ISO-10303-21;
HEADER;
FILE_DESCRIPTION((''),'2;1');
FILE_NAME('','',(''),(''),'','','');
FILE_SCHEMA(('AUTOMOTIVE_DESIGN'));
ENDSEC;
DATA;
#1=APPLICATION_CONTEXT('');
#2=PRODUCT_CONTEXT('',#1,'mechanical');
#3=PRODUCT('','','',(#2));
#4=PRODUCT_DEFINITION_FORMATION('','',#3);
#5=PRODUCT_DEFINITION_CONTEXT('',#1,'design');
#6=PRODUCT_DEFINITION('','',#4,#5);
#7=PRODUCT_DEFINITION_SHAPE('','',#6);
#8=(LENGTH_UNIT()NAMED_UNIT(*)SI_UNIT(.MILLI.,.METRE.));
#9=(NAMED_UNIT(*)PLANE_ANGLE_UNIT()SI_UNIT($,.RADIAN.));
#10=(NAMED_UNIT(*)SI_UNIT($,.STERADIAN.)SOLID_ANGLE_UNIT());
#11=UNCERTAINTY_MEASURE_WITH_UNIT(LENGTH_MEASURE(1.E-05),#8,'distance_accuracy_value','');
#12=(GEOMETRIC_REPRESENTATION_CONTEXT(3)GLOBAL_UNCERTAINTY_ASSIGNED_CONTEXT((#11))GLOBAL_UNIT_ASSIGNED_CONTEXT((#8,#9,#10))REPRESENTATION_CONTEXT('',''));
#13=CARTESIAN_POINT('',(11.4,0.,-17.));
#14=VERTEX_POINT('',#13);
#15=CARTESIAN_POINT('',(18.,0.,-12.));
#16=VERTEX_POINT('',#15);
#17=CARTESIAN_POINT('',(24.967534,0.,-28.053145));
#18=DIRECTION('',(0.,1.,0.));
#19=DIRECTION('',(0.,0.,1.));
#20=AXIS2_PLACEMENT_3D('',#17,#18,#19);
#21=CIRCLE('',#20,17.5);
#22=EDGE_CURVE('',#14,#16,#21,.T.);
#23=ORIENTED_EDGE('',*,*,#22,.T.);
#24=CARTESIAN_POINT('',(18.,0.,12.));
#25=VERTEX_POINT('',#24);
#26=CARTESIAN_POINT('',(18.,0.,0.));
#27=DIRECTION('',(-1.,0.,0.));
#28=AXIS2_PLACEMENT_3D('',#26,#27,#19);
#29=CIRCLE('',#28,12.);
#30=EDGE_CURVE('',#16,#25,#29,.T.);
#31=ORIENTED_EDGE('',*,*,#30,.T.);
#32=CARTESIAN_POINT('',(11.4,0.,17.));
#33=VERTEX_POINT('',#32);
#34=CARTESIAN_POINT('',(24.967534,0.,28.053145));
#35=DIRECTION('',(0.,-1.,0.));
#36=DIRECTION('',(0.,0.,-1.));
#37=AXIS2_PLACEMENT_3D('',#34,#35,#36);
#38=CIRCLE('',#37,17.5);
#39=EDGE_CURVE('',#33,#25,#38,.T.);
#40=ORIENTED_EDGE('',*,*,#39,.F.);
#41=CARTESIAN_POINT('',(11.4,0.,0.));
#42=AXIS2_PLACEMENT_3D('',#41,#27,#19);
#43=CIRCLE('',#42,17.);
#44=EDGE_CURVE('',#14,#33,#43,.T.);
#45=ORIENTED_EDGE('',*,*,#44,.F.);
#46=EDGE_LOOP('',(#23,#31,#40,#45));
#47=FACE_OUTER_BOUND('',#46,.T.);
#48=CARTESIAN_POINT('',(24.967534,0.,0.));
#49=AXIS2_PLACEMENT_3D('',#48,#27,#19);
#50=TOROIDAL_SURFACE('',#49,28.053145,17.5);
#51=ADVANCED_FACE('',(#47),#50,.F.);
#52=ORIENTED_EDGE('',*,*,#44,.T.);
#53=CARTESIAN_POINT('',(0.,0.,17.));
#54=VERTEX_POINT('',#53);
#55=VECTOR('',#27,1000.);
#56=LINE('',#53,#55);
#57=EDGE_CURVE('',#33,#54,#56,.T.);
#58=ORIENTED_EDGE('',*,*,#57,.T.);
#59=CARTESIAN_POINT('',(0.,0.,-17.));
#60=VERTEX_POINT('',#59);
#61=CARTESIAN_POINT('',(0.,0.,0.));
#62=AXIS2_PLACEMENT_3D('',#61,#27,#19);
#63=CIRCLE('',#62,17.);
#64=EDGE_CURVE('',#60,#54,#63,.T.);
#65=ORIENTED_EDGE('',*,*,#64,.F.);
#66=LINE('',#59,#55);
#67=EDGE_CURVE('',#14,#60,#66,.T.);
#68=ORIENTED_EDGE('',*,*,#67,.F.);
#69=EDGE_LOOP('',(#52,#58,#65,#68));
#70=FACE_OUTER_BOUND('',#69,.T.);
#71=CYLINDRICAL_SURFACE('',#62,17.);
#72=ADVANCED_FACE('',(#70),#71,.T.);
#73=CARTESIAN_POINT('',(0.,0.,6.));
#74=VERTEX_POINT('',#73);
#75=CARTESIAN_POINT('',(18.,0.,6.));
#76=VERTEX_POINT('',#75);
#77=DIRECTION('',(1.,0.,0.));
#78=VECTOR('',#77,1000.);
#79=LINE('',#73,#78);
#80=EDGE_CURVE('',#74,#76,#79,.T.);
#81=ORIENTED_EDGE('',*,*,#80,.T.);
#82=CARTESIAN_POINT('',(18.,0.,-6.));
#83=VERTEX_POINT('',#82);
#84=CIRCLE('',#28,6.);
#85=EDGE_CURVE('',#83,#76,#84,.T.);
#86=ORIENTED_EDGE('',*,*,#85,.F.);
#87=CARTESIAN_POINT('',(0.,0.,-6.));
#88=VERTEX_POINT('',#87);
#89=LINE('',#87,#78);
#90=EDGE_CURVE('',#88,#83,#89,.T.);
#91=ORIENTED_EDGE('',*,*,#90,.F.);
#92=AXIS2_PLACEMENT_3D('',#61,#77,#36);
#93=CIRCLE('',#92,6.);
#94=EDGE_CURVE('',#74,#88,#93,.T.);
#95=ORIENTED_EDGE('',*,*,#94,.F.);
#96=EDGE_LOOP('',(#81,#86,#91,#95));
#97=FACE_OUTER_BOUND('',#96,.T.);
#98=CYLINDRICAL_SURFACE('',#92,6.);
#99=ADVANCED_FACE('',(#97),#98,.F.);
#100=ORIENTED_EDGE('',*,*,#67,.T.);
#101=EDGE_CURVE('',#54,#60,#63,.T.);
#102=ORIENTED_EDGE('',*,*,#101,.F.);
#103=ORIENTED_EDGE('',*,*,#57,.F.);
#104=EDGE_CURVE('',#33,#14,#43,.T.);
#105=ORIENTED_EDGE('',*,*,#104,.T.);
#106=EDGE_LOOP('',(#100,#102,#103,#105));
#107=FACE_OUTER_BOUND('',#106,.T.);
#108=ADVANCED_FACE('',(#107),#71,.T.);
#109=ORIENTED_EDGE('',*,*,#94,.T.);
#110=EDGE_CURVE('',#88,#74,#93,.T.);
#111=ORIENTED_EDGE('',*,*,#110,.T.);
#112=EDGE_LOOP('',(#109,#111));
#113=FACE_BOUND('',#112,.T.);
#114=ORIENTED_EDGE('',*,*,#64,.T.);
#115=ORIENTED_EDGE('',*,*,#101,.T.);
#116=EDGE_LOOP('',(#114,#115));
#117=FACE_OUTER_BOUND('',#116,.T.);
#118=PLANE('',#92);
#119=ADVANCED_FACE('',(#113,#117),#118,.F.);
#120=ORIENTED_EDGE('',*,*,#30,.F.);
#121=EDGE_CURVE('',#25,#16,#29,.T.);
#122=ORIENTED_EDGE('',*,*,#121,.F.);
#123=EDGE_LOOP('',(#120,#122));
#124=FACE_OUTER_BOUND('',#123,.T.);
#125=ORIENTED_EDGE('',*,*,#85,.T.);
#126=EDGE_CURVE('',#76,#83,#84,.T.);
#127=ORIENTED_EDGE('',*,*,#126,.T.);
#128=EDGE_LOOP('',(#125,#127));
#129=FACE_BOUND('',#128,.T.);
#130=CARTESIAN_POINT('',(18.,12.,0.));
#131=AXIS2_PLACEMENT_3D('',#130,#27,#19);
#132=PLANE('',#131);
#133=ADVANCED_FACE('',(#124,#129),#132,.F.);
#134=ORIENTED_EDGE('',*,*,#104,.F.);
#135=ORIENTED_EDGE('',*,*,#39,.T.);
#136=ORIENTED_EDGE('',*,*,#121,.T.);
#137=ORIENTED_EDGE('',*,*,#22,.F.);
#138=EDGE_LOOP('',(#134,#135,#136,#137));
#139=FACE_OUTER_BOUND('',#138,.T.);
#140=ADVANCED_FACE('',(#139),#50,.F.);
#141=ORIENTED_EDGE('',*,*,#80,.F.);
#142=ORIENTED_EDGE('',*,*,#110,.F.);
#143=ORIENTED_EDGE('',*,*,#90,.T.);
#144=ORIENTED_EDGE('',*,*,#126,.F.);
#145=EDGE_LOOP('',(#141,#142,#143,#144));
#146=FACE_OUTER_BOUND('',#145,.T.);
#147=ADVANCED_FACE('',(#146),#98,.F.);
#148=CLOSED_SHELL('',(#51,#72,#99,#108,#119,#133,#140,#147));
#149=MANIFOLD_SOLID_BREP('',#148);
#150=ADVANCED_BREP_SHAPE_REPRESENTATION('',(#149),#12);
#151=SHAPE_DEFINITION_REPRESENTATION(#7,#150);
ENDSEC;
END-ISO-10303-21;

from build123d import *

# Parameters (mm, degrees)
CUT_EXTRUDE1_DEPTH      = 31.033314835
CUT_EXTRUDE1_DEPTH_BACK = 31.033314835
SKETCH2_R               = 6


with BuildPart() as part:
    # Sketch1 → Revolve1 (revolve)
    with BuildSketch(Plane.XY, mode=Mode.PRIVATE) as revolve1_sk:
        with BuildLine():
            Line((0, 0), (0, 17))
            Line((0, 17), (11.4, 17))
            ThreePointArc((11.4, 17), (14.400024627, 14.104032508), (18, 12))
            Line((18, 12), (18, 0))
            Line((18, 0), (0, 0))
        make_face()
    revolve(revolve1_sk.sketch.rotate(Axis((0, 0, 0), (1, 0, 0)), 90), axis=Axis((0, 0, 0), (1, 0, 0)))

    # Sketch2 → Cut-Extrude1 (cut, two sides: drawn at the far end of the back side and taken through both)
    with BuildSketch(Plane(origin=(18, 0, 0), x_dir=(0, 0, -1), z_dir=(1, 0, 0)).offset(-CUT_EXTRUDE1_DEPTH_BACK)):
        Circle(SKETCH2_R)
    extrude(amount=CUT_EXTRUDE1_DEPTH + CUT_EXTRUDE1_DEPTH_BACK, mode=Mode.SUBTRACT)


solid = part.part
